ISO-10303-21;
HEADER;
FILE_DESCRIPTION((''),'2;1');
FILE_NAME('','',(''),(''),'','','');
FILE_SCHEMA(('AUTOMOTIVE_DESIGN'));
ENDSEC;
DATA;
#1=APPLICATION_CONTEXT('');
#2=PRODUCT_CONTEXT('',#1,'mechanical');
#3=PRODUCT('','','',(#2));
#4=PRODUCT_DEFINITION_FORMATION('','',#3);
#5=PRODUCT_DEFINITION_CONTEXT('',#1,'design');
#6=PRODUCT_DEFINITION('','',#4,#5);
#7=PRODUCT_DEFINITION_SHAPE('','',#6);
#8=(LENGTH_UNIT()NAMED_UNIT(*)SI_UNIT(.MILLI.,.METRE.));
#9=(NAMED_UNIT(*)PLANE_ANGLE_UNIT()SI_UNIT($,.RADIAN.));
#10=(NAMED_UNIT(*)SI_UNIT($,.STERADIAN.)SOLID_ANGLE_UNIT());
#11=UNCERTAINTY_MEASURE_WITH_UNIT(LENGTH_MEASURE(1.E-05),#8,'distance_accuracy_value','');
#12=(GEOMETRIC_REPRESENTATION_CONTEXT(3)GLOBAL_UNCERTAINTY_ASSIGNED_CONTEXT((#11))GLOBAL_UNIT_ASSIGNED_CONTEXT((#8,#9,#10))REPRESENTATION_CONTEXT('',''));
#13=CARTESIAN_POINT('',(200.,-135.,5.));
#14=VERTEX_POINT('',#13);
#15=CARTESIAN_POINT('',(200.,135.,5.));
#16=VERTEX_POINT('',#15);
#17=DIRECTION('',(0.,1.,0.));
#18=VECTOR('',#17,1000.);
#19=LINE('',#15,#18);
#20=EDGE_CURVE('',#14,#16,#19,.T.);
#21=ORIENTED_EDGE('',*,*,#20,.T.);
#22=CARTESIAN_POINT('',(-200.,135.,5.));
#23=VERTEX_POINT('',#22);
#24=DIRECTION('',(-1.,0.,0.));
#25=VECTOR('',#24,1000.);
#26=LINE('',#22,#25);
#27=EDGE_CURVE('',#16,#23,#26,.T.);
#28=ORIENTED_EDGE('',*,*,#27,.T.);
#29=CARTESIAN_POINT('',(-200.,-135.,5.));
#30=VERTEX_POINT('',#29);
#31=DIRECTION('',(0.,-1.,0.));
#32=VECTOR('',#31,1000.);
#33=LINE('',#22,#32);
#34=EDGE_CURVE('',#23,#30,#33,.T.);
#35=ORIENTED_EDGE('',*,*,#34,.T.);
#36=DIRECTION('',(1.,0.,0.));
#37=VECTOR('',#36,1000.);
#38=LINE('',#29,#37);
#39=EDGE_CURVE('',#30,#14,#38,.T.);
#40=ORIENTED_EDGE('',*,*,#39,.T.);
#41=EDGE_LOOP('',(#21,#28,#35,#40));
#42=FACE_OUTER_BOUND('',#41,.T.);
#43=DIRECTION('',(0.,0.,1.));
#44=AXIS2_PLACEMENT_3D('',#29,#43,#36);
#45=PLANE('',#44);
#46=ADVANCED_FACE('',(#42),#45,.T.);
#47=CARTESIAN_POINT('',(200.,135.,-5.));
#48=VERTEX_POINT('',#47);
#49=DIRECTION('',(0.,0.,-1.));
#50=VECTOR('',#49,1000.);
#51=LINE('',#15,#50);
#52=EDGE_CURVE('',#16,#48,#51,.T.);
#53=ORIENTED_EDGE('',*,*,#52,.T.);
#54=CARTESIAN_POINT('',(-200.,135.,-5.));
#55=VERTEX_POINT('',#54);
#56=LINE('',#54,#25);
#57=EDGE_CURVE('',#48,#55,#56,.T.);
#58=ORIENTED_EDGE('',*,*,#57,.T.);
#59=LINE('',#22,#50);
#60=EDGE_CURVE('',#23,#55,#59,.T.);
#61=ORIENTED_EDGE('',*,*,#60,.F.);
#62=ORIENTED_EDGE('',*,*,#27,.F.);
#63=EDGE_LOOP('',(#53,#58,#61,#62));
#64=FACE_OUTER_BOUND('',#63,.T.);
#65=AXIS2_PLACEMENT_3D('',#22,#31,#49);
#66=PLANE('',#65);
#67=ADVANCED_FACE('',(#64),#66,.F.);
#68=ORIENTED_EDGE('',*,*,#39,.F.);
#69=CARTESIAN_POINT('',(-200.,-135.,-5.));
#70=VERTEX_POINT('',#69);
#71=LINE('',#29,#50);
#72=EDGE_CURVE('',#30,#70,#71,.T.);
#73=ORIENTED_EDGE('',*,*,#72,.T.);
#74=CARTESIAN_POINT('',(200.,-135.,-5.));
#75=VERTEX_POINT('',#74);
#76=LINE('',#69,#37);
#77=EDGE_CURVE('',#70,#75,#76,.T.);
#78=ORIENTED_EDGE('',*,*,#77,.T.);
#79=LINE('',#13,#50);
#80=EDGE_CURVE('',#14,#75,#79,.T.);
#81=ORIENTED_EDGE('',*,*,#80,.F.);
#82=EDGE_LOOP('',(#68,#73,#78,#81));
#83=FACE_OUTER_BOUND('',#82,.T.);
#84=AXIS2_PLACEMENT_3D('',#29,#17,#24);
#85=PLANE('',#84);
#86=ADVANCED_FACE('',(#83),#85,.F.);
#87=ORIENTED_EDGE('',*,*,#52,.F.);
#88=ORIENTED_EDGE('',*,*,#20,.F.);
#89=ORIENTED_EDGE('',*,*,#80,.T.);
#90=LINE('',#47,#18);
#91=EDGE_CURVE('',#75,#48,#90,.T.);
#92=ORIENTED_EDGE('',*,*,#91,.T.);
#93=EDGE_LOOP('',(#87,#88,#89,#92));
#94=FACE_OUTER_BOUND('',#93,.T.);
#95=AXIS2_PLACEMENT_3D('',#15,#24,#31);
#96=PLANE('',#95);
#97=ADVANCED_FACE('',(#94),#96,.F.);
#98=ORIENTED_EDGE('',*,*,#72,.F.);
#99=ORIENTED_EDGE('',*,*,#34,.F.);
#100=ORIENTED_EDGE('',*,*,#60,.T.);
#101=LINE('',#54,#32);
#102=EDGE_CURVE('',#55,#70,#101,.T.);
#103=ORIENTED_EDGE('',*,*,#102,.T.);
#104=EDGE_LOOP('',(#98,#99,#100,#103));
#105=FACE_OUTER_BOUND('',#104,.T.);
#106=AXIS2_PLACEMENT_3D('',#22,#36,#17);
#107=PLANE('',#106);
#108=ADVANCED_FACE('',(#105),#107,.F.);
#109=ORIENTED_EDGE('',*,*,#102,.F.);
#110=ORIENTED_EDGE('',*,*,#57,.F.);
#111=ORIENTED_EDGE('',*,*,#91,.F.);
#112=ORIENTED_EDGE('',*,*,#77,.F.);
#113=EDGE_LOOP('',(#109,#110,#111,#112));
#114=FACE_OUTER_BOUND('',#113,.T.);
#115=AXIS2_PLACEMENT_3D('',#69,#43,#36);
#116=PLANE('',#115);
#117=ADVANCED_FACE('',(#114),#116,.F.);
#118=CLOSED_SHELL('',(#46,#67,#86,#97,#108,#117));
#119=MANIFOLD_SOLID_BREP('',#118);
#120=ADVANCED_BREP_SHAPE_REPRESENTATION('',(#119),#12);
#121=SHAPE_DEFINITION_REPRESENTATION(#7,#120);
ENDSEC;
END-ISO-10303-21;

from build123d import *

# Parameters (mm, degrees)
SKETCH1_W           = 400
SKETCH1_H           = 270
BOSS_EXTRUDE1_DEPTH = 5


with BuildPart() as part:
    # Sketch1 → Boss-Extrude1 (new, symmetric)
    with BuildSketch(Plane.XY):
        Rectangle(SKETCH1_W, SKETCH1_H)
    extrude(amount=BOSS_EXTRUDE1_DEPTH, both=True)


solid = part.part
